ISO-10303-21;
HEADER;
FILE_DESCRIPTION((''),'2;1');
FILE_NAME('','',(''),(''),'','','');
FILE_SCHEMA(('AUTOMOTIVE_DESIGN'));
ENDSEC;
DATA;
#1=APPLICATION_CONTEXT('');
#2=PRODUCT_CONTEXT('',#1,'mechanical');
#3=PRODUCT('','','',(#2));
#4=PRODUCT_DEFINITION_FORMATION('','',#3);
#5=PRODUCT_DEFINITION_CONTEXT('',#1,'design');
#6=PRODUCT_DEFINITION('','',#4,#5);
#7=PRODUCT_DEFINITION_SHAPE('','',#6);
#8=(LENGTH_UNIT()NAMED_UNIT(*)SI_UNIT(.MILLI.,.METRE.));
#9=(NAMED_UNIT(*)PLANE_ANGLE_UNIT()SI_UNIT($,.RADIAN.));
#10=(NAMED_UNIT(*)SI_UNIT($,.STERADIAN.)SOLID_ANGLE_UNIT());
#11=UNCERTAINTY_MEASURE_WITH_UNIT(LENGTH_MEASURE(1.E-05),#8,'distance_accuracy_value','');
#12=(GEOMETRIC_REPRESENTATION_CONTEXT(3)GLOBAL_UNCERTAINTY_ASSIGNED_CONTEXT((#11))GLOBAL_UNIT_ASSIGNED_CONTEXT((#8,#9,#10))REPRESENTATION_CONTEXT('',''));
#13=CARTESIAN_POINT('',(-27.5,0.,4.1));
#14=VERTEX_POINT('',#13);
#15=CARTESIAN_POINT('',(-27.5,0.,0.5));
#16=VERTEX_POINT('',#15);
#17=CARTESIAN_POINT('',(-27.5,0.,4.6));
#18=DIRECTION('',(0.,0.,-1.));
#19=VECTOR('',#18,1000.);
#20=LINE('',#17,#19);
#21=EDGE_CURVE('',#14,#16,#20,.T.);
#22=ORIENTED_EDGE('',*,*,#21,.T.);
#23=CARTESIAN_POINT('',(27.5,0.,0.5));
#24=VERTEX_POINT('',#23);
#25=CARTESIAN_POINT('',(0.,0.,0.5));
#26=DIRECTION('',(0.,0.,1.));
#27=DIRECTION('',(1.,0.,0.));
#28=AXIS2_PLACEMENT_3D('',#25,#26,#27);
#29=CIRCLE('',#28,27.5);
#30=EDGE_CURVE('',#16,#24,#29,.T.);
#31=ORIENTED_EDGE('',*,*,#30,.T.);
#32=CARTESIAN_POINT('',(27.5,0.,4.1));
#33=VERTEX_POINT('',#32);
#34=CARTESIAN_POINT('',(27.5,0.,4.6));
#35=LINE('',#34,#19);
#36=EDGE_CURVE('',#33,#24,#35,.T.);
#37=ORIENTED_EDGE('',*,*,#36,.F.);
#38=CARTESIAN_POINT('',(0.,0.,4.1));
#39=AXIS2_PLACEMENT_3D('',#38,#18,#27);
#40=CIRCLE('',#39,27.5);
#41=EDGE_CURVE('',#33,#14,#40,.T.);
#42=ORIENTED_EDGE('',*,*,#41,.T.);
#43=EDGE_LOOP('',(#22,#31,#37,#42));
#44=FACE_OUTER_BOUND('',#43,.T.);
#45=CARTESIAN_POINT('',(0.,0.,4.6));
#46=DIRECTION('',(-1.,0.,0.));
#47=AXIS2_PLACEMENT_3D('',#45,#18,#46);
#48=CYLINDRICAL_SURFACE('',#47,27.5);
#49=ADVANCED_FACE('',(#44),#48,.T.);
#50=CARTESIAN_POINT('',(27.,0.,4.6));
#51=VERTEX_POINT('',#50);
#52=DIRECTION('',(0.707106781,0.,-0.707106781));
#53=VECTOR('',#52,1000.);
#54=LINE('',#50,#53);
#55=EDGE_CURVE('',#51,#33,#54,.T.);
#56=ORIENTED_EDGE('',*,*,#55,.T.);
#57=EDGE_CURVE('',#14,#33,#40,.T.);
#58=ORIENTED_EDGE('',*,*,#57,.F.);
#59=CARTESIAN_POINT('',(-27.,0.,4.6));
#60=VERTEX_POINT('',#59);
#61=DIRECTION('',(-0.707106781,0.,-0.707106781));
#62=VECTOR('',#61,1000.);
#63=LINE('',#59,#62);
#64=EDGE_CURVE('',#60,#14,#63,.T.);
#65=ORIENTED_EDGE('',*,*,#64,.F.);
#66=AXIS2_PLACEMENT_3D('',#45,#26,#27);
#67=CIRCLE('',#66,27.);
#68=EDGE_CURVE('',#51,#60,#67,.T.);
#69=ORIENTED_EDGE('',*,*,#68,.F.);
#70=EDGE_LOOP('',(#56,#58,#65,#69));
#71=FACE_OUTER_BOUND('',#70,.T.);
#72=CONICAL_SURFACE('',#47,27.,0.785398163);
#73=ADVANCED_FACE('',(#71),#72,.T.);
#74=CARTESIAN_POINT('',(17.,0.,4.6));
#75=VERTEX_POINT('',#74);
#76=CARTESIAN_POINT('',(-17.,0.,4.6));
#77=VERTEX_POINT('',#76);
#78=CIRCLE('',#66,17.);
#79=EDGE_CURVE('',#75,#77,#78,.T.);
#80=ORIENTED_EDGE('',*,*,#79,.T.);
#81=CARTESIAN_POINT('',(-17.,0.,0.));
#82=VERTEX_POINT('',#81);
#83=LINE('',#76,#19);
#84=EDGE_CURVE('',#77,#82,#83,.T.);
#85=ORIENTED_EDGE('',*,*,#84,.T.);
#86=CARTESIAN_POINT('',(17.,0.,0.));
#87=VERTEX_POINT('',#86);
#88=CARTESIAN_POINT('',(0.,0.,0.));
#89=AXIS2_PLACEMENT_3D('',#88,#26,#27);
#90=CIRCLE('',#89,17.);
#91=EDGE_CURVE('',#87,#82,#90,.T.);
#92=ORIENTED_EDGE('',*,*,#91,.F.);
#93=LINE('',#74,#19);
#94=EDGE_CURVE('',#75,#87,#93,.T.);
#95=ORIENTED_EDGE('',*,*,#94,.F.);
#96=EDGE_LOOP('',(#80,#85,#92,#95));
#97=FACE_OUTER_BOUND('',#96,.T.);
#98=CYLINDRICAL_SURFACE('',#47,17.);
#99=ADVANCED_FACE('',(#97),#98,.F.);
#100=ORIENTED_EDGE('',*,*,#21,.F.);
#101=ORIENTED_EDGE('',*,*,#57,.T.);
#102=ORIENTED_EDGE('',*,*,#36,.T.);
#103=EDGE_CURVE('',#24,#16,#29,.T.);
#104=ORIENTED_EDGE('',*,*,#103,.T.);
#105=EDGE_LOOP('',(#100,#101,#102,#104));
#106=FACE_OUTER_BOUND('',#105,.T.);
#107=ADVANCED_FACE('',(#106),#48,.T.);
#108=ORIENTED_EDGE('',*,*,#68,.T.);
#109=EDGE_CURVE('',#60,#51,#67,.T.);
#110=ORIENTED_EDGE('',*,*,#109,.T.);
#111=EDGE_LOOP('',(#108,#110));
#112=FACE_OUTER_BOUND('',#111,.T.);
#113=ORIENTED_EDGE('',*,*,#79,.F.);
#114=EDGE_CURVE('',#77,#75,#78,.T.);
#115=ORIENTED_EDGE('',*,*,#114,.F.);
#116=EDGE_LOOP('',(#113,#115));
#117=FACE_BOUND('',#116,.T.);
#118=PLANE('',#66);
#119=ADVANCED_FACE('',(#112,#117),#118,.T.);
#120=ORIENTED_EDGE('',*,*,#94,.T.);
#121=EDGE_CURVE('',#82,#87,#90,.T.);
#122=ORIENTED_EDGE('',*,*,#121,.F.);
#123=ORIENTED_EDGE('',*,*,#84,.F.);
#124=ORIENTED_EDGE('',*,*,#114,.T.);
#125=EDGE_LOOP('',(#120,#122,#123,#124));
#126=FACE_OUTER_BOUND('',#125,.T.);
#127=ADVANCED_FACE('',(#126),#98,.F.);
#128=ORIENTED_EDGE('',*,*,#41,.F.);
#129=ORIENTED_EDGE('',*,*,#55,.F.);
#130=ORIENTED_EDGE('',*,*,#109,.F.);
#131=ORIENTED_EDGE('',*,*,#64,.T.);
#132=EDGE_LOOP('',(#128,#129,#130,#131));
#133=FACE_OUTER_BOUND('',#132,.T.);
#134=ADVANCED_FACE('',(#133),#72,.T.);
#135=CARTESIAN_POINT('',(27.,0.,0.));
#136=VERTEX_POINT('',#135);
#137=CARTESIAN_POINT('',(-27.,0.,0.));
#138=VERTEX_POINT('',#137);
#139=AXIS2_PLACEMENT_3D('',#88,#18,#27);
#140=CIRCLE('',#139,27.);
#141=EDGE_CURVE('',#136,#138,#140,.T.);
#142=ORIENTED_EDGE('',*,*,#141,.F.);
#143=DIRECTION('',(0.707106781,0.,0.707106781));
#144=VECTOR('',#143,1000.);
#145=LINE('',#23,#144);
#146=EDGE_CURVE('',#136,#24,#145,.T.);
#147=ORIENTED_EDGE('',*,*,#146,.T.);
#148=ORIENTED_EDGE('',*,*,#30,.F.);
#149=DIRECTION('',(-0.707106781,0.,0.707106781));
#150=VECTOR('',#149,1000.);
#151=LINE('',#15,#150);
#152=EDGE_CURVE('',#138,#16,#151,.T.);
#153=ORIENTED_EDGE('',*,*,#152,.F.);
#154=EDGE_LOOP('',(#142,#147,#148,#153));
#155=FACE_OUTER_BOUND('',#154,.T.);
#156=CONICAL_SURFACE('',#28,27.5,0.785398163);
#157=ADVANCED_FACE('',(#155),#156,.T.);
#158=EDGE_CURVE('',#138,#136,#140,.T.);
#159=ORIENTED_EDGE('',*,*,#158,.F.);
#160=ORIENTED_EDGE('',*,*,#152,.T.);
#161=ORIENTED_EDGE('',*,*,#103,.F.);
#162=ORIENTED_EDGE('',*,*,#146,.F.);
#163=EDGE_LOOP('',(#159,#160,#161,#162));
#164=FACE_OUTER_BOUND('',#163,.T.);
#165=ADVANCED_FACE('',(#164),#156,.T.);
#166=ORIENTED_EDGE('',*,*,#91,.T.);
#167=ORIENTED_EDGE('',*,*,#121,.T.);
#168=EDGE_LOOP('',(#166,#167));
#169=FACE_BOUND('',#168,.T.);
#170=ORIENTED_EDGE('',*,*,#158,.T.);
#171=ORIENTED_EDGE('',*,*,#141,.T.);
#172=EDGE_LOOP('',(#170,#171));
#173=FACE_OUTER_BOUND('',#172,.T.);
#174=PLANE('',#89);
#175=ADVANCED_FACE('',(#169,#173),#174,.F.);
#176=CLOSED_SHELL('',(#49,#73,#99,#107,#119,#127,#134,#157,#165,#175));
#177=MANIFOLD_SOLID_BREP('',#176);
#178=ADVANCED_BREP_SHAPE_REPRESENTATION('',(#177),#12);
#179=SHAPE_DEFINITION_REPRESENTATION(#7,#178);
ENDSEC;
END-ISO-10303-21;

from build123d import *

# Parameters (mm, degrees)
SKETCH_1_R      = 27.5
SKETCH_1_R_2    = 17
EXTRUDE_1_DEPTH = 4.6
CHAMFER_1_SIZE  = 0.5


with BuildPart() as part:
    # 草图1 → 凸台-拉伸1 (new body)
    with BuildSketch(Plane.XY):
        Circle(SKETCH_1_R)
        Circle(SKETCH_1_R_2, mode=Mode.SUBTRACT)
    extrude(amount=EXTRUDE_1_DEPTH)

    # 倒角1
    chamfer_1_edges = [part.edges().sort_by_distance(p)[0] for p in [
        (-27.5, 0, 0),
        (-27.5, 0, 4.6),
    ]]
    chamfer(chamfer_1_edges, length=CHAMFER_1_SIZE)


solid = part.part
